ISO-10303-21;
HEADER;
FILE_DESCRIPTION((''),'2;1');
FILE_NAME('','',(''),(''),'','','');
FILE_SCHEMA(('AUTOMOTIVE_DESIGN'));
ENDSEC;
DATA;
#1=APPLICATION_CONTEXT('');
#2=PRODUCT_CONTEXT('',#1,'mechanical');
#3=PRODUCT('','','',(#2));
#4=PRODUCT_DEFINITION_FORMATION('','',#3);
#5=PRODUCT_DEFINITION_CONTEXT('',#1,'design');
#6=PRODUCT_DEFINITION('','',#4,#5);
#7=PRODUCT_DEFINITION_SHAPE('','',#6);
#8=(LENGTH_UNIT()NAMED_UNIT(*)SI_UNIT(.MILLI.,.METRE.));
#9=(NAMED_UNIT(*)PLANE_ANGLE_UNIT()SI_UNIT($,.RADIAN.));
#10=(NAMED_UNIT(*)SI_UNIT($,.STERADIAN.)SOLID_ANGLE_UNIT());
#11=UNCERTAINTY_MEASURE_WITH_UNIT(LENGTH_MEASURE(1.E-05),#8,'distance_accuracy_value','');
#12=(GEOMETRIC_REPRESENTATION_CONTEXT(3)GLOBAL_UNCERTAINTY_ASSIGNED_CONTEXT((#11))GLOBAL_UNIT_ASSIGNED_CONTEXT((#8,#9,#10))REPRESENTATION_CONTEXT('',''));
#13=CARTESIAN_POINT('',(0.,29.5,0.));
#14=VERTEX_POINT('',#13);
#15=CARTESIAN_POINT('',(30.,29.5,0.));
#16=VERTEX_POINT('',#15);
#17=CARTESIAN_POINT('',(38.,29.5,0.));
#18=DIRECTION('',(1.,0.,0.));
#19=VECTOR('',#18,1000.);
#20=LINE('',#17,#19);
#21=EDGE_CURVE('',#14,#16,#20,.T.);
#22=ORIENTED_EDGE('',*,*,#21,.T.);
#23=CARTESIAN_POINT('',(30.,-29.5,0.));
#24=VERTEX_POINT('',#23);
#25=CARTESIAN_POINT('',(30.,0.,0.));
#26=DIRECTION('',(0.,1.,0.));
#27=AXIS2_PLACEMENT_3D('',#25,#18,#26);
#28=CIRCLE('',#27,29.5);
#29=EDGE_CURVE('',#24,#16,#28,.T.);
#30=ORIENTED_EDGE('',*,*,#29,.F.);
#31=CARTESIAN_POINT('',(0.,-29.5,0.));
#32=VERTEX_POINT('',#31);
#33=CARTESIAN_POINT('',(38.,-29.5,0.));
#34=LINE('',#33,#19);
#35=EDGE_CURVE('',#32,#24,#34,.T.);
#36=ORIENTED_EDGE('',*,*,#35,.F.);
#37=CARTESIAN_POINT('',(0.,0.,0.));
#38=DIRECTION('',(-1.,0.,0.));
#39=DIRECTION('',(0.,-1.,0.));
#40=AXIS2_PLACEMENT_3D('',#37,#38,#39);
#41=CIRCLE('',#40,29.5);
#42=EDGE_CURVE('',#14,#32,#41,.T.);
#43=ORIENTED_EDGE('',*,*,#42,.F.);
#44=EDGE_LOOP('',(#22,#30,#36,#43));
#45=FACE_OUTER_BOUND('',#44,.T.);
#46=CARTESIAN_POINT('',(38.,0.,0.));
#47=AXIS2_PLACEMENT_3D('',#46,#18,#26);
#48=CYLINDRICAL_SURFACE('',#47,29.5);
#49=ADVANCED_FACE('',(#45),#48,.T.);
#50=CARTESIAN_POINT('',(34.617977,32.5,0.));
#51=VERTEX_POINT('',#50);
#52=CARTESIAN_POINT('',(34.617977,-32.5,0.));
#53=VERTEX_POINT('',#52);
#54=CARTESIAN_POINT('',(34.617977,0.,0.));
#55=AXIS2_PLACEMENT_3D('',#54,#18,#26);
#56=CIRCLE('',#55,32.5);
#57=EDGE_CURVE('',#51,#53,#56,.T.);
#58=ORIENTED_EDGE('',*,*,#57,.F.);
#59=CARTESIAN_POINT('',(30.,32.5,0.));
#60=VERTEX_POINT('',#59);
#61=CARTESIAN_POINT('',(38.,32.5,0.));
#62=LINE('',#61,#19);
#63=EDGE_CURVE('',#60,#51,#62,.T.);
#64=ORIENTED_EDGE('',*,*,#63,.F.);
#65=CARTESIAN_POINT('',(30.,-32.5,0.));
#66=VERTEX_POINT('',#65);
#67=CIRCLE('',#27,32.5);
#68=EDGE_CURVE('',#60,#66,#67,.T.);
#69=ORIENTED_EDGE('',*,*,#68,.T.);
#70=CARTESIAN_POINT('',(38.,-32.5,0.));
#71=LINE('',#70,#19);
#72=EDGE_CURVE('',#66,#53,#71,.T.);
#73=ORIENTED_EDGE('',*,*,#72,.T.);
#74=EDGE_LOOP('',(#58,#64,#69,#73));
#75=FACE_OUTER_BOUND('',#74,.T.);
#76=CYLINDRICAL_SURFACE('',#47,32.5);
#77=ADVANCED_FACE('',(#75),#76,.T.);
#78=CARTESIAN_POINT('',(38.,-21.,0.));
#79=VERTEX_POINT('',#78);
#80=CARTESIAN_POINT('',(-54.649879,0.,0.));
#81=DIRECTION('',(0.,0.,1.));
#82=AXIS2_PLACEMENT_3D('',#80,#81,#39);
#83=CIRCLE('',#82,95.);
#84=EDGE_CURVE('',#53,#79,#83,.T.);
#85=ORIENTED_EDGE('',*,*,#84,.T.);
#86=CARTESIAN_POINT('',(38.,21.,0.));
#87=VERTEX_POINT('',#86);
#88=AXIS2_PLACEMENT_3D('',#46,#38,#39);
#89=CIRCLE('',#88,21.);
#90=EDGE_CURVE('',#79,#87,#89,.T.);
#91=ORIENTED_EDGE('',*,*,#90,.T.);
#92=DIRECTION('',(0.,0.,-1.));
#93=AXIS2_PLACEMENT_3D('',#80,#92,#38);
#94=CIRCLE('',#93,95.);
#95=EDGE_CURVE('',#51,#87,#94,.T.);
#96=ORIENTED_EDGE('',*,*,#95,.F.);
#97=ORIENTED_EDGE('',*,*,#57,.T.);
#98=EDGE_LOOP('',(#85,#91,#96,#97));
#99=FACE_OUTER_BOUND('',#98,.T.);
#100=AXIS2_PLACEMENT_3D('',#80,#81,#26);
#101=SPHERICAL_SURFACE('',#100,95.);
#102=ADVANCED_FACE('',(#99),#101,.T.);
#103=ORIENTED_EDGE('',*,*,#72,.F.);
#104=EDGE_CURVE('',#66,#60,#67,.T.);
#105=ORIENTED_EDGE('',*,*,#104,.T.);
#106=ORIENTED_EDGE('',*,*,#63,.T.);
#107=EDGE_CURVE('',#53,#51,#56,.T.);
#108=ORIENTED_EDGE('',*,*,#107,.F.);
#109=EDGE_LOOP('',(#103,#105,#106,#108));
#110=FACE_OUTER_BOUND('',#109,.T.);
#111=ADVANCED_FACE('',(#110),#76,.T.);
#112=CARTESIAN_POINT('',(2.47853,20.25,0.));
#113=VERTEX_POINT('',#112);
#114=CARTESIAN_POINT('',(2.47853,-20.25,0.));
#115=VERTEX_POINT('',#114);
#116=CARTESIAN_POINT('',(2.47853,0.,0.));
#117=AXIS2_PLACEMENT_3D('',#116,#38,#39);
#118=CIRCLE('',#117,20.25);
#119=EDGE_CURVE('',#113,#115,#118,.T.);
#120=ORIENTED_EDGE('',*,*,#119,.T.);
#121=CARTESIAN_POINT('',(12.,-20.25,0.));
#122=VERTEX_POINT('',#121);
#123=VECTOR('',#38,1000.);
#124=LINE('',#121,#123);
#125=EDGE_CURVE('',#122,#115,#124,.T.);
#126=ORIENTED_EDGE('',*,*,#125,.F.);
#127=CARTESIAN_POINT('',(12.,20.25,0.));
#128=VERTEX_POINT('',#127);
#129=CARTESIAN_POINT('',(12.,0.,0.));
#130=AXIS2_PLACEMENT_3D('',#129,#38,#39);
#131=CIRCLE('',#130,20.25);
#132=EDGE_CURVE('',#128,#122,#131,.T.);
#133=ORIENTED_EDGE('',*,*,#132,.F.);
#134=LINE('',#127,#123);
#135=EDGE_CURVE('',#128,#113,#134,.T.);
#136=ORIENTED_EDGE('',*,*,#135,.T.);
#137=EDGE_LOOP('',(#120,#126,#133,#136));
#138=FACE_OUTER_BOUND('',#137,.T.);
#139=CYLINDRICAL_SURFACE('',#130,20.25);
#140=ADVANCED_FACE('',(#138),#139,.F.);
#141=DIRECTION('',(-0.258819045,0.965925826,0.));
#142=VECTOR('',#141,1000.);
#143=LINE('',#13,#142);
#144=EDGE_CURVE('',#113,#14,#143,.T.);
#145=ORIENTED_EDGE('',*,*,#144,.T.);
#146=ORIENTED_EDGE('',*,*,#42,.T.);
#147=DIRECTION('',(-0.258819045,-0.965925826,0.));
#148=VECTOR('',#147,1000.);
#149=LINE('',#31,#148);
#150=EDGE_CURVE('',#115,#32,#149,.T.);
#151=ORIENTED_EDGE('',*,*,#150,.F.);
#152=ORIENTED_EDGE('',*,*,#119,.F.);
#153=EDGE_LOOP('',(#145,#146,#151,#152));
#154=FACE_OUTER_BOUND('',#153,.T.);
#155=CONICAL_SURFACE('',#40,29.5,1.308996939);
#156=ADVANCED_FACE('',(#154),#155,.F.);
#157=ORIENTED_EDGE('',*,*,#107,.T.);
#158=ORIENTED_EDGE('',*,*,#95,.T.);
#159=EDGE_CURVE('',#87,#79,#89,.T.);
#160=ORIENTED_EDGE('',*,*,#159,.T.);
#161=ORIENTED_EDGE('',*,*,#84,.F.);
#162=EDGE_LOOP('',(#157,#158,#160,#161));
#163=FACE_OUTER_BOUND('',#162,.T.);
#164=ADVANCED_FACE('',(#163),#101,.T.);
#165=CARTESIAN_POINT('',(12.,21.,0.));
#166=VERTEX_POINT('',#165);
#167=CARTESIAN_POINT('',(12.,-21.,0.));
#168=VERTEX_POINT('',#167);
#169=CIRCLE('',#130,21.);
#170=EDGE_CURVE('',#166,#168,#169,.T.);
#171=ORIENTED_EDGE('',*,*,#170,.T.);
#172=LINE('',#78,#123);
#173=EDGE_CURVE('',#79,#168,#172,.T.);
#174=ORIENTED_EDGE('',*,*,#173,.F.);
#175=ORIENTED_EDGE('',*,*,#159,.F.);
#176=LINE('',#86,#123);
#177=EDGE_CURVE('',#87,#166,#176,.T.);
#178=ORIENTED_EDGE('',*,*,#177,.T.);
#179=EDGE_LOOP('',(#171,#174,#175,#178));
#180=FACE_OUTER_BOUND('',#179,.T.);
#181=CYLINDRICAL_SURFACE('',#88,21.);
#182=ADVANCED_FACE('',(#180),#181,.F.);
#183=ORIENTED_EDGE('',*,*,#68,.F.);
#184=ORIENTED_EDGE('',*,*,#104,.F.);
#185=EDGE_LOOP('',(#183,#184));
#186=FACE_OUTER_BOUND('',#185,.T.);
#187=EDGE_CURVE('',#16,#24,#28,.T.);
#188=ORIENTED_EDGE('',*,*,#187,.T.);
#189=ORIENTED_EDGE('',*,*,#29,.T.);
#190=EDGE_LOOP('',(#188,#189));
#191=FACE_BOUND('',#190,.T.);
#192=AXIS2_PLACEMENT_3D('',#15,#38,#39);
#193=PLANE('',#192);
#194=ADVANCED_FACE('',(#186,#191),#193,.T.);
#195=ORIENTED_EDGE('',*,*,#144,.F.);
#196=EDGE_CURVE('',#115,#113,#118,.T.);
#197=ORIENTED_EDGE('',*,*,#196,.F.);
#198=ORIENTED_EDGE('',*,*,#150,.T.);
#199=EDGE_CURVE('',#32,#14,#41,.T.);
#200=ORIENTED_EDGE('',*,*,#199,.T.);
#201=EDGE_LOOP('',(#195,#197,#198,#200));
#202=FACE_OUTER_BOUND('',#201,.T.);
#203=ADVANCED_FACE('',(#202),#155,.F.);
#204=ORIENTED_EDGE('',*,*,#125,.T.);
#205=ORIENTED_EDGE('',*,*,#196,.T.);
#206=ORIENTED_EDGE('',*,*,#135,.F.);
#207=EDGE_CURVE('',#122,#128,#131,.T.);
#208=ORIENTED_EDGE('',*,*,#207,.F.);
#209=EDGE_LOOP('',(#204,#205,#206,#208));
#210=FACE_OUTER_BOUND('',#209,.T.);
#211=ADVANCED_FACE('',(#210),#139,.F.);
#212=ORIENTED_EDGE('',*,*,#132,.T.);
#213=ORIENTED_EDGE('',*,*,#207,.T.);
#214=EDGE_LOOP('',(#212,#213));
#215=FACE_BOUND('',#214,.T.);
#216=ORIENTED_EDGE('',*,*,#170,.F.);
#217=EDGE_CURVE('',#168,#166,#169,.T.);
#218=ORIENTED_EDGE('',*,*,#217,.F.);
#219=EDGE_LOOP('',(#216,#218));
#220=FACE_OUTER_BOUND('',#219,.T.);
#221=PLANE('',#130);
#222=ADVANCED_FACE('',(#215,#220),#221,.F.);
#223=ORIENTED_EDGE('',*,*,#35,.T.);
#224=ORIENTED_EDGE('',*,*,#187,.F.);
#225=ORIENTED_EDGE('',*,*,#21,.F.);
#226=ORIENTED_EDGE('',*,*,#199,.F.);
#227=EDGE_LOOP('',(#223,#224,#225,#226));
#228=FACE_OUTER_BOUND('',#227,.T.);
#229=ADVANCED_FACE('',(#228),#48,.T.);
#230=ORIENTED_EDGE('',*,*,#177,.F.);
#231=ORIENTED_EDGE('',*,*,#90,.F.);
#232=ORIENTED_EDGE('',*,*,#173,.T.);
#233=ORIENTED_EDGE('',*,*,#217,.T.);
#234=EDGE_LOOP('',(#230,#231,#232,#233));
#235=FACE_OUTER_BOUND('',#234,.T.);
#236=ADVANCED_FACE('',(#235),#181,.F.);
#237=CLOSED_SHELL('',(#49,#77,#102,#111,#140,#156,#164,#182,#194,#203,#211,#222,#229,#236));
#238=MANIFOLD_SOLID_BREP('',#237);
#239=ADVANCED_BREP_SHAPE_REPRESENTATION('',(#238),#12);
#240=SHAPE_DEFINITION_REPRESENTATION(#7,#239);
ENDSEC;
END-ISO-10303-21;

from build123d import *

# Parameters (mm, degrees)
SKETCH3_R          = 20.25
CUT_EXTRUDE2_DEPTH = 12
SKETCH4_R          = 21
CUT_EXTRUDE3_DEPTH = 53.80624963


with BuildPart() as part:
    # Sketch1 → Revolve1 (revolve)
    with BuildSketch(Plane.XY):
        with BuildLine():
            Line((0, 0), (0, 29.5))
            Line((0, 29.5), (30, 29.5))
            Line((30, 29.5), (30, 32.5))
            Line((30, 32.5), (34.617976782, 32.5))
            ThreePointArc((34.617976782, 32.5), (36.49055142, 26.803395685), (38, 21))
            Line((38, 21), (38, 0))
            Line((38, 0), (0, 0))
        make_face()
    revolve(axis=Axis((38, 0, 0), (-1, 0, 0)))

    # Sketch3 → Cut-Extrude2 (cut)
    with BuildSketch(Plane.ZY):
        with Locations(Location((0, 0, 0), (0, 0, 270))):
            Circle(SKETCH3_R)
    extrude(amount=-CUT_EXTRUDE2_DEPTH, mode=Mode.SUBTRACT)

    # Cut-Extrude1 cone 1 section (through the dimple's axis) → Cut-Extrude1 (revolve, cut)
    with BuildSketch(Plane.ZX):
        Polygon((0, 0), (29.5, 0), (0, 7.904501177), align=None)
    revolve(axis=Axis((0, 0, 0), (1, 0, 0)), mode=Mode.SUBTRACT)

    # Sketch4 → Cut-Extrude3 (cut, through all)
    with BuildSketch(Plane.ZY.offset(-12)):
        with Locations(Location((0, 0, 0), (0, 0, 270))):
            Circle(SKETCH4_R)
    extrude(amount=-CUT_EXTRUDE3_DEPTH, mode=Mode.SUBTRACT)


solid = part.part
